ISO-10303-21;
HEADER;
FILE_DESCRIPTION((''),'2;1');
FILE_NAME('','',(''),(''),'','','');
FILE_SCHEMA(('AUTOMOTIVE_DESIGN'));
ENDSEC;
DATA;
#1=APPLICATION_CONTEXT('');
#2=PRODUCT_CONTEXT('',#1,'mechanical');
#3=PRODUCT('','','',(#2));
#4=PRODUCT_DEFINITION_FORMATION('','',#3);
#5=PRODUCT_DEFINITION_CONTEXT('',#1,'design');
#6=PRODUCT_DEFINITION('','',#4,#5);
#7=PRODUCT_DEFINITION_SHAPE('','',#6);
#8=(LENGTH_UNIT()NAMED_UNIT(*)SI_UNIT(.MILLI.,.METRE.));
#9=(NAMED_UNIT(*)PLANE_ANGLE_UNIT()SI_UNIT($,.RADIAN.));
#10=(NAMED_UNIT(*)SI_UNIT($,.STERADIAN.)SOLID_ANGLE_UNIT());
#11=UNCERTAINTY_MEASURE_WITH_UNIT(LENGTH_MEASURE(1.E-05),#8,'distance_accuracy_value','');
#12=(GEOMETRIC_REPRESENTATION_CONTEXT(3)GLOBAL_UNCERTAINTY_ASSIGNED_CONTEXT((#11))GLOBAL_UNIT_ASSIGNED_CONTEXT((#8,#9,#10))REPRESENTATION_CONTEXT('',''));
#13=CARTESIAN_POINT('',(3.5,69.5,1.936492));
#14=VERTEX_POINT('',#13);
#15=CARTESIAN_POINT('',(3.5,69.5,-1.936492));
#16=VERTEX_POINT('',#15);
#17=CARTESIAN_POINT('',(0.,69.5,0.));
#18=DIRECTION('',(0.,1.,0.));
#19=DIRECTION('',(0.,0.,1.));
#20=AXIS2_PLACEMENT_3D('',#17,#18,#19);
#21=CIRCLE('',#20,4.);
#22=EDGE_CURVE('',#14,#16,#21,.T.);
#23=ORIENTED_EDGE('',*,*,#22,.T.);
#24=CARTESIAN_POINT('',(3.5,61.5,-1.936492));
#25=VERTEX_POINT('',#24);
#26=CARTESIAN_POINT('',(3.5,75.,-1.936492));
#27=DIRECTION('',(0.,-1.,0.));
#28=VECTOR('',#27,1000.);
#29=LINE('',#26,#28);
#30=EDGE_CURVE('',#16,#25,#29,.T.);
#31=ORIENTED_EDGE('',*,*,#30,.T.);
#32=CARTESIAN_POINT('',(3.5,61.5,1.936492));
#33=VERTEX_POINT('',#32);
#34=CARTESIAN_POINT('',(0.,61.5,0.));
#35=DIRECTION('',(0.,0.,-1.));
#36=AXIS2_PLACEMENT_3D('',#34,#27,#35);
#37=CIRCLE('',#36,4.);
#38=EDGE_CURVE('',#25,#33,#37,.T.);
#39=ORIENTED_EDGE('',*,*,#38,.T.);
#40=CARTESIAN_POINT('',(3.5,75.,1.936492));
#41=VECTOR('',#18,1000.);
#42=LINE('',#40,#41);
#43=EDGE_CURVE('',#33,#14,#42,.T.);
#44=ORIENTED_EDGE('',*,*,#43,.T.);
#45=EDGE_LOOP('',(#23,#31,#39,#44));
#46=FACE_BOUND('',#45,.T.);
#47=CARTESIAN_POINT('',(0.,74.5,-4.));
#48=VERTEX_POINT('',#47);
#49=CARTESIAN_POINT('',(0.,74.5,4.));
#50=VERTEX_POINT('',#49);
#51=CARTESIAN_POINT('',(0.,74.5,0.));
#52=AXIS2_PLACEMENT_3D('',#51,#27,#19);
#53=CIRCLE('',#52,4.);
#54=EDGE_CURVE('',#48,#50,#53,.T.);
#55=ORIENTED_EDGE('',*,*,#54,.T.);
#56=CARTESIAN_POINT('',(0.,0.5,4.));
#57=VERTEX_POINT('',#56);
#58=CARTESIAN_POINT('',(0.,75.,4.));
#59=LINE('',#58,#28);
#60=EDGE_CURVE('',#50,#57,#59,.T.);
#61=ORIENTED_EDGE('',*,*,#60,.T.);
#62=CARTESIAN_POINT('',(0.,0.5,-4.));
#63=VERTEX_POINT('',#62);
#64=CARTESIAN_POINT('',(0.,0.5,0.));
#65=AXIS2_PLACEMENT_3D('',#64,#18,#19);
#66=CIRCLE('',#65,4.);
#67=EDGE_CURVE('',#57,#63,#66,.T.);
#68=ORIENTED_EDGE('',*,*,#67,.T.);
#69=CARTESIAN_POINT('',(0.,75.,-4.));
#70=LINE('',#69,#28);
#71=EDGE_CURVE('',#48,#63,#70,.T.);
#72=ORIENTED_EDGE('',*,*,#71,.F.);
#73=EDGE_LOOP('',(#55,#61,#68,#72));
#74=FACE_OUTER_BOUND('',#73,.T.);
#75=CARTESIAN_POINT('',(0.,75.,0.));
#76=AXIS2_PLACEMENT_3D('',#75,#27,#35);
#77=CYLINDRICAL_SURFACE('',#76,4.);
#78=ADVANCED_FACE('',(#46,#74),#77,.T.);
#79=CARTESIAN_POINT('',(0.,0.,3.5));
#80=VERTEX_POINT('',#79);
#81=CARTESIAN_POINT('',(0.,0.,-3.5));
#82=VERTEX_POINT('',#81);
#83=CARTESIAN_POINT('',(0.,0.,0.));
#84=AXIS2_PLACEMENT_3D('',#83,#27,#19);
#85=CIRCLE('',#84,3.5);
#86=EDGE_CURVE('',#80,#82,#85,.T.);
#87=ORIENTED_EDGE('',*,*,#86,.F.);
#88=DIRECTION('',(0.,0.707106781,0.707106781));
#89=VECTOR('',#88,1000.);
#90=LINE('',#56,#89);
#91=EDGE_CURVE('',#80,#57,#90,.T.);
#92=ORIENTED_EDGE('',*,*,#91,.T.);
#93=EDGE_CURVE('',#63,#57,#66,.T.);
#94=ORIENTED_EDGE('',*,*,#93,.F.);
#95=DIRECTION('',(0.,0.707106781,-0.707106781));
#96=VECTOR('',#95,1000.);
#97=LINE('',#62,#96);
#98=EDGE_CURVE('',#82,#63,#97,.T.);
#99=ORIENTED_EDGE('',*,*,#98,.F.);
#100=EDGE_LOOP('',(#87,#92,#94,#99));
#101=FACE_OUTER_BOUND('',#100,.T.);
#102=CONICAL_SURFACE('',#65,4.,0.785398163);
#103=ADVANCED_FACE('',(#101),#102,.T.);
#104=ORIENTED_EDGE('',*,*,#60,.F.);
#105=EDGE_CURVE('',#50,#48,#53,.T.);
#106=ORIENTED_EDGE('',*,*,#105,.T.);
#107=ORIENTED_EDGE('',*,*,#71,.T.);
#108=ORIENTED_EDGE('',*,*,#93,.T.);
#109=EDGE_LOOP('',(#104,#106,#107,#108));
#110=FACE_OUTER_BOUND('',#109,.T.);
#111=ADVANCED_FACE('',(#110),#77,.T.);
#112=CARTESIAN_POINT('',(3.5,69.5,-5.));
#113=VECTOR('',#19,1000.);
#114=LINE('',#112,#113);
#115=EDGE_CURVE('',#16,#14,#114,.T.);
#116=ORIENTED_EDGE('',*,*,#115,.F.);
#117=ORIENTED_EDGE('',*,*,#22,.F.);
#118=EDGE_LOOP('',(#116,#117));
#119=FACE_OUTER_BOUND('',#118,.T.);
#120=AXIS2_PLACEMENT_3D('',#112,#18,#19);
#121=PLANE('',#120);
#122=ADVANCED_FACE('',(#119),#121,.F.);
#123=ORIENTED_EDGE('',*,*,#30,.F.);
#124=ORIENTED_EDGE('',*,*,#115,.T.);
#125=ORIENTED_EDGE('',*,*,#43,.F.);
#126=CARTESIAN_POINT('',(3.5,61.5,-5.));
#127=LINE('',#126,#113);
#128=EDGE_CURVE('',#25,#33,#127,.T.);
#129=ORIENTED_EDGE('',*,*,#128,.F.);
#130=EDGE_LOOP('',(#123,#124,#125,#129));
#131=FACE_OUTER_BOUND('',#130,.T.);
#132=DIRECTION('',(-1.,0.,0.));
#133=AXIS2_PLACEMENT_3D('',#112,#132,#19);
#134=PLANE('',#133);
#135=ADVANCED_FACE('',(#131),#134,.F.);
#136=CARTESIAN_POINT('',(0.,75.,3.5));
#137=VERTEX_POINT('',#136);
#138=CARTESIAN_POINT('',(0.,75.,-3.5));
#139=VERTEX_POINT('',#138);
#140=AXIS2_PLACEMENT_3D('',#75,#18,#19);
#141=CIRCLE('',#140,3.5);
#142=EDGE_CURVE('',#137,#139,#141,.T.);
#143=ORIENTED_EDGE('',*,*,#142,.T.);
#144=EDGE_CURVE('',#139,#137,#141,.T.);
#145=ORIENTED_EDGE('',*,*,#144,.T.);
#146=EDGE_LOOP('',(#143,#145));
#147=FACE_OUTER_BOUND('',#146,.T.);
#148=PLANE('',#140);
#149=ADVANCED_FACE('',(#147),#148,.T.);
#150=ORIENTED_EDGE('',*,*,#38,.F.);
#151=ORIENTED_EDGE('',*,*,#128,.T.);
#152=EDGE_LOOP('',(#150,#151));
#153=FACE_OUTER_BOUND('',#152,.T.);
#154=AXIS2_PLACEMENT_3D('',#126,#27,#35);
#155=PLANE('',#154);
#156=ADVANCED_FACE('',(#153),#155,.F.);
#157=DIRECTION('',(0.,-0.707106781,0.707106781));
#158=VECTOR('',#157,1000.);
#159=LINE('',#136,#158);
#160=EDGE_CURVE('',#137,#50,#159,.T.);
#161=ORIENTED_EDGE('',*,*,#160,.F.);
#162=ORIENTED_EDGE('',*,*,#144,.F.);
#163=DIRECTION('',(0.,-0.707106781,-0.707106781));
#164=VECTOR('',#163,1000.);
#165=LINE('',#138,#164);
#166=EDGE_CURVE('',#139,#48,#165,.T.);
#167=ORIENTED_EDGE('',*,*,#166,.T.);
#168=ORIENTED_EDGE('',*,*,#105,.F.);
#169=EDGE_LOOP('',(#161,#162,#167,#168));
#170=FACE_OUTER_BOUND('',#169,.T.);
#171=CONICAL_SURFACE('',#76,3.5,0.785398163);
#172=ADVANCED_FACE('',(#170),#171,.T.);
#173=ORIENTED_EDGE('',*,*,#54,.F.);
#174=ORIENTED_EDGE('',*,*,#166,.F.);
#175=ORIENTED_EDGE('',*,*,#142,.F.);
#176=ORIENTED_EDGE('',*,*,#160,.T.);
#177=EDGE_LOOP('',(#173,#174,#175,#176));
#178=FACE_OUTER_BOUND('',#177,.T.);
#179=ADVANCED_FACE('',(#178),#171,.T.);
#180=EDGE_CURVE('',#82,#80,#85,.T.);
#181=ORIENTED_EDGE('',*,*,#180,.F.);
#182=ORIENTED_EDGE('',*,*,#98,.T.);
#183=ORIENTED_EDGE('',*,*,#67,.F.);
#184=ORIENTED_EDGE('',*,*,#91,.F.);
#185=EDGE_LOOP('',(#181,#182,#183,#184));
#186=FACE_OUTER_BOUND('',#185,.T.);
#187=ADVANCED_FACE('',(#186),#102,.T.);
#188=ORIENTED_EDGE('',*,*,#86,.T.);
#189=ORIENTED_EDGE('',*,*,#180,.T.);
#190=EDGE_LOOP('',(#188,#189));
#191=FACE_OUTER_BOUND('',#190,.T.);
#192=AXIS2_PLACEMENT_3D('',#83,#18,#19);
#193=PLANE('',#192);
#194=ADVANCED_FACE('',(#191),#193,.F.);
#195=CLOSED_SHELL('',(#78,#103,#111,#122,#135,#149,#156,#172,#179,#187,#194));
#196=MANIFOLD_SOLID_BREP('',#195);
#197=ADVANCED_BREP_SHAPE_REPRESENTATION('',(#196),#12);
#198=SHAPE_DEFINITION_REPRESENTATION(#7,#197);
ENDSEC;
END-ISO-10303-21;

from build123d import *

# Parameters (mm, degrees)
SKETCH1_R           = 4
BOSS_EXTRUDE1_DEPTH = 75
CHAMFER1_SIZE       = 0.5
SKETCH2_W           = 1
SKETCH2_H           = 8
CUT_EXTRUDE1_DEPTH  = 5


with BuildPart() as part:
    # Sketch1 → Boss-Extrude1 (new body)
    with BuildSketch(Plane(origin=(0, 0, 0), x_dir=(1, 0, 0), z_dir=(0, 1, 0))):
        with Locations(Location((0, 0, 0), (0, 0, 270))):
            Circle(SKETCH1_R)
    extrude(amount=BOSS_EXTRUDE1_DEPTH)

    # Chamfer1
    chamfer1_edges = [part.edges().sort_by_distance(p)[0] for p in [
        (0, 0, -4),
        (0, 75, -4),
    ]]
    chamfer(chamfer1_edges, length=CHAMFER1_SIZE)

    # Sketch2 → Cut-Extrude1 (cut, symmetric)
    with BuildSketch(Plane.XY):
        with Locations((4, 65.5)):
            Rectangle(SKETCH2_W, SKETCH2_H)
    extrude(amount=CUT_EXTRUDE1_DEPTH, both=True, mode=Mode.SUBTRACT)


solid = part.part
